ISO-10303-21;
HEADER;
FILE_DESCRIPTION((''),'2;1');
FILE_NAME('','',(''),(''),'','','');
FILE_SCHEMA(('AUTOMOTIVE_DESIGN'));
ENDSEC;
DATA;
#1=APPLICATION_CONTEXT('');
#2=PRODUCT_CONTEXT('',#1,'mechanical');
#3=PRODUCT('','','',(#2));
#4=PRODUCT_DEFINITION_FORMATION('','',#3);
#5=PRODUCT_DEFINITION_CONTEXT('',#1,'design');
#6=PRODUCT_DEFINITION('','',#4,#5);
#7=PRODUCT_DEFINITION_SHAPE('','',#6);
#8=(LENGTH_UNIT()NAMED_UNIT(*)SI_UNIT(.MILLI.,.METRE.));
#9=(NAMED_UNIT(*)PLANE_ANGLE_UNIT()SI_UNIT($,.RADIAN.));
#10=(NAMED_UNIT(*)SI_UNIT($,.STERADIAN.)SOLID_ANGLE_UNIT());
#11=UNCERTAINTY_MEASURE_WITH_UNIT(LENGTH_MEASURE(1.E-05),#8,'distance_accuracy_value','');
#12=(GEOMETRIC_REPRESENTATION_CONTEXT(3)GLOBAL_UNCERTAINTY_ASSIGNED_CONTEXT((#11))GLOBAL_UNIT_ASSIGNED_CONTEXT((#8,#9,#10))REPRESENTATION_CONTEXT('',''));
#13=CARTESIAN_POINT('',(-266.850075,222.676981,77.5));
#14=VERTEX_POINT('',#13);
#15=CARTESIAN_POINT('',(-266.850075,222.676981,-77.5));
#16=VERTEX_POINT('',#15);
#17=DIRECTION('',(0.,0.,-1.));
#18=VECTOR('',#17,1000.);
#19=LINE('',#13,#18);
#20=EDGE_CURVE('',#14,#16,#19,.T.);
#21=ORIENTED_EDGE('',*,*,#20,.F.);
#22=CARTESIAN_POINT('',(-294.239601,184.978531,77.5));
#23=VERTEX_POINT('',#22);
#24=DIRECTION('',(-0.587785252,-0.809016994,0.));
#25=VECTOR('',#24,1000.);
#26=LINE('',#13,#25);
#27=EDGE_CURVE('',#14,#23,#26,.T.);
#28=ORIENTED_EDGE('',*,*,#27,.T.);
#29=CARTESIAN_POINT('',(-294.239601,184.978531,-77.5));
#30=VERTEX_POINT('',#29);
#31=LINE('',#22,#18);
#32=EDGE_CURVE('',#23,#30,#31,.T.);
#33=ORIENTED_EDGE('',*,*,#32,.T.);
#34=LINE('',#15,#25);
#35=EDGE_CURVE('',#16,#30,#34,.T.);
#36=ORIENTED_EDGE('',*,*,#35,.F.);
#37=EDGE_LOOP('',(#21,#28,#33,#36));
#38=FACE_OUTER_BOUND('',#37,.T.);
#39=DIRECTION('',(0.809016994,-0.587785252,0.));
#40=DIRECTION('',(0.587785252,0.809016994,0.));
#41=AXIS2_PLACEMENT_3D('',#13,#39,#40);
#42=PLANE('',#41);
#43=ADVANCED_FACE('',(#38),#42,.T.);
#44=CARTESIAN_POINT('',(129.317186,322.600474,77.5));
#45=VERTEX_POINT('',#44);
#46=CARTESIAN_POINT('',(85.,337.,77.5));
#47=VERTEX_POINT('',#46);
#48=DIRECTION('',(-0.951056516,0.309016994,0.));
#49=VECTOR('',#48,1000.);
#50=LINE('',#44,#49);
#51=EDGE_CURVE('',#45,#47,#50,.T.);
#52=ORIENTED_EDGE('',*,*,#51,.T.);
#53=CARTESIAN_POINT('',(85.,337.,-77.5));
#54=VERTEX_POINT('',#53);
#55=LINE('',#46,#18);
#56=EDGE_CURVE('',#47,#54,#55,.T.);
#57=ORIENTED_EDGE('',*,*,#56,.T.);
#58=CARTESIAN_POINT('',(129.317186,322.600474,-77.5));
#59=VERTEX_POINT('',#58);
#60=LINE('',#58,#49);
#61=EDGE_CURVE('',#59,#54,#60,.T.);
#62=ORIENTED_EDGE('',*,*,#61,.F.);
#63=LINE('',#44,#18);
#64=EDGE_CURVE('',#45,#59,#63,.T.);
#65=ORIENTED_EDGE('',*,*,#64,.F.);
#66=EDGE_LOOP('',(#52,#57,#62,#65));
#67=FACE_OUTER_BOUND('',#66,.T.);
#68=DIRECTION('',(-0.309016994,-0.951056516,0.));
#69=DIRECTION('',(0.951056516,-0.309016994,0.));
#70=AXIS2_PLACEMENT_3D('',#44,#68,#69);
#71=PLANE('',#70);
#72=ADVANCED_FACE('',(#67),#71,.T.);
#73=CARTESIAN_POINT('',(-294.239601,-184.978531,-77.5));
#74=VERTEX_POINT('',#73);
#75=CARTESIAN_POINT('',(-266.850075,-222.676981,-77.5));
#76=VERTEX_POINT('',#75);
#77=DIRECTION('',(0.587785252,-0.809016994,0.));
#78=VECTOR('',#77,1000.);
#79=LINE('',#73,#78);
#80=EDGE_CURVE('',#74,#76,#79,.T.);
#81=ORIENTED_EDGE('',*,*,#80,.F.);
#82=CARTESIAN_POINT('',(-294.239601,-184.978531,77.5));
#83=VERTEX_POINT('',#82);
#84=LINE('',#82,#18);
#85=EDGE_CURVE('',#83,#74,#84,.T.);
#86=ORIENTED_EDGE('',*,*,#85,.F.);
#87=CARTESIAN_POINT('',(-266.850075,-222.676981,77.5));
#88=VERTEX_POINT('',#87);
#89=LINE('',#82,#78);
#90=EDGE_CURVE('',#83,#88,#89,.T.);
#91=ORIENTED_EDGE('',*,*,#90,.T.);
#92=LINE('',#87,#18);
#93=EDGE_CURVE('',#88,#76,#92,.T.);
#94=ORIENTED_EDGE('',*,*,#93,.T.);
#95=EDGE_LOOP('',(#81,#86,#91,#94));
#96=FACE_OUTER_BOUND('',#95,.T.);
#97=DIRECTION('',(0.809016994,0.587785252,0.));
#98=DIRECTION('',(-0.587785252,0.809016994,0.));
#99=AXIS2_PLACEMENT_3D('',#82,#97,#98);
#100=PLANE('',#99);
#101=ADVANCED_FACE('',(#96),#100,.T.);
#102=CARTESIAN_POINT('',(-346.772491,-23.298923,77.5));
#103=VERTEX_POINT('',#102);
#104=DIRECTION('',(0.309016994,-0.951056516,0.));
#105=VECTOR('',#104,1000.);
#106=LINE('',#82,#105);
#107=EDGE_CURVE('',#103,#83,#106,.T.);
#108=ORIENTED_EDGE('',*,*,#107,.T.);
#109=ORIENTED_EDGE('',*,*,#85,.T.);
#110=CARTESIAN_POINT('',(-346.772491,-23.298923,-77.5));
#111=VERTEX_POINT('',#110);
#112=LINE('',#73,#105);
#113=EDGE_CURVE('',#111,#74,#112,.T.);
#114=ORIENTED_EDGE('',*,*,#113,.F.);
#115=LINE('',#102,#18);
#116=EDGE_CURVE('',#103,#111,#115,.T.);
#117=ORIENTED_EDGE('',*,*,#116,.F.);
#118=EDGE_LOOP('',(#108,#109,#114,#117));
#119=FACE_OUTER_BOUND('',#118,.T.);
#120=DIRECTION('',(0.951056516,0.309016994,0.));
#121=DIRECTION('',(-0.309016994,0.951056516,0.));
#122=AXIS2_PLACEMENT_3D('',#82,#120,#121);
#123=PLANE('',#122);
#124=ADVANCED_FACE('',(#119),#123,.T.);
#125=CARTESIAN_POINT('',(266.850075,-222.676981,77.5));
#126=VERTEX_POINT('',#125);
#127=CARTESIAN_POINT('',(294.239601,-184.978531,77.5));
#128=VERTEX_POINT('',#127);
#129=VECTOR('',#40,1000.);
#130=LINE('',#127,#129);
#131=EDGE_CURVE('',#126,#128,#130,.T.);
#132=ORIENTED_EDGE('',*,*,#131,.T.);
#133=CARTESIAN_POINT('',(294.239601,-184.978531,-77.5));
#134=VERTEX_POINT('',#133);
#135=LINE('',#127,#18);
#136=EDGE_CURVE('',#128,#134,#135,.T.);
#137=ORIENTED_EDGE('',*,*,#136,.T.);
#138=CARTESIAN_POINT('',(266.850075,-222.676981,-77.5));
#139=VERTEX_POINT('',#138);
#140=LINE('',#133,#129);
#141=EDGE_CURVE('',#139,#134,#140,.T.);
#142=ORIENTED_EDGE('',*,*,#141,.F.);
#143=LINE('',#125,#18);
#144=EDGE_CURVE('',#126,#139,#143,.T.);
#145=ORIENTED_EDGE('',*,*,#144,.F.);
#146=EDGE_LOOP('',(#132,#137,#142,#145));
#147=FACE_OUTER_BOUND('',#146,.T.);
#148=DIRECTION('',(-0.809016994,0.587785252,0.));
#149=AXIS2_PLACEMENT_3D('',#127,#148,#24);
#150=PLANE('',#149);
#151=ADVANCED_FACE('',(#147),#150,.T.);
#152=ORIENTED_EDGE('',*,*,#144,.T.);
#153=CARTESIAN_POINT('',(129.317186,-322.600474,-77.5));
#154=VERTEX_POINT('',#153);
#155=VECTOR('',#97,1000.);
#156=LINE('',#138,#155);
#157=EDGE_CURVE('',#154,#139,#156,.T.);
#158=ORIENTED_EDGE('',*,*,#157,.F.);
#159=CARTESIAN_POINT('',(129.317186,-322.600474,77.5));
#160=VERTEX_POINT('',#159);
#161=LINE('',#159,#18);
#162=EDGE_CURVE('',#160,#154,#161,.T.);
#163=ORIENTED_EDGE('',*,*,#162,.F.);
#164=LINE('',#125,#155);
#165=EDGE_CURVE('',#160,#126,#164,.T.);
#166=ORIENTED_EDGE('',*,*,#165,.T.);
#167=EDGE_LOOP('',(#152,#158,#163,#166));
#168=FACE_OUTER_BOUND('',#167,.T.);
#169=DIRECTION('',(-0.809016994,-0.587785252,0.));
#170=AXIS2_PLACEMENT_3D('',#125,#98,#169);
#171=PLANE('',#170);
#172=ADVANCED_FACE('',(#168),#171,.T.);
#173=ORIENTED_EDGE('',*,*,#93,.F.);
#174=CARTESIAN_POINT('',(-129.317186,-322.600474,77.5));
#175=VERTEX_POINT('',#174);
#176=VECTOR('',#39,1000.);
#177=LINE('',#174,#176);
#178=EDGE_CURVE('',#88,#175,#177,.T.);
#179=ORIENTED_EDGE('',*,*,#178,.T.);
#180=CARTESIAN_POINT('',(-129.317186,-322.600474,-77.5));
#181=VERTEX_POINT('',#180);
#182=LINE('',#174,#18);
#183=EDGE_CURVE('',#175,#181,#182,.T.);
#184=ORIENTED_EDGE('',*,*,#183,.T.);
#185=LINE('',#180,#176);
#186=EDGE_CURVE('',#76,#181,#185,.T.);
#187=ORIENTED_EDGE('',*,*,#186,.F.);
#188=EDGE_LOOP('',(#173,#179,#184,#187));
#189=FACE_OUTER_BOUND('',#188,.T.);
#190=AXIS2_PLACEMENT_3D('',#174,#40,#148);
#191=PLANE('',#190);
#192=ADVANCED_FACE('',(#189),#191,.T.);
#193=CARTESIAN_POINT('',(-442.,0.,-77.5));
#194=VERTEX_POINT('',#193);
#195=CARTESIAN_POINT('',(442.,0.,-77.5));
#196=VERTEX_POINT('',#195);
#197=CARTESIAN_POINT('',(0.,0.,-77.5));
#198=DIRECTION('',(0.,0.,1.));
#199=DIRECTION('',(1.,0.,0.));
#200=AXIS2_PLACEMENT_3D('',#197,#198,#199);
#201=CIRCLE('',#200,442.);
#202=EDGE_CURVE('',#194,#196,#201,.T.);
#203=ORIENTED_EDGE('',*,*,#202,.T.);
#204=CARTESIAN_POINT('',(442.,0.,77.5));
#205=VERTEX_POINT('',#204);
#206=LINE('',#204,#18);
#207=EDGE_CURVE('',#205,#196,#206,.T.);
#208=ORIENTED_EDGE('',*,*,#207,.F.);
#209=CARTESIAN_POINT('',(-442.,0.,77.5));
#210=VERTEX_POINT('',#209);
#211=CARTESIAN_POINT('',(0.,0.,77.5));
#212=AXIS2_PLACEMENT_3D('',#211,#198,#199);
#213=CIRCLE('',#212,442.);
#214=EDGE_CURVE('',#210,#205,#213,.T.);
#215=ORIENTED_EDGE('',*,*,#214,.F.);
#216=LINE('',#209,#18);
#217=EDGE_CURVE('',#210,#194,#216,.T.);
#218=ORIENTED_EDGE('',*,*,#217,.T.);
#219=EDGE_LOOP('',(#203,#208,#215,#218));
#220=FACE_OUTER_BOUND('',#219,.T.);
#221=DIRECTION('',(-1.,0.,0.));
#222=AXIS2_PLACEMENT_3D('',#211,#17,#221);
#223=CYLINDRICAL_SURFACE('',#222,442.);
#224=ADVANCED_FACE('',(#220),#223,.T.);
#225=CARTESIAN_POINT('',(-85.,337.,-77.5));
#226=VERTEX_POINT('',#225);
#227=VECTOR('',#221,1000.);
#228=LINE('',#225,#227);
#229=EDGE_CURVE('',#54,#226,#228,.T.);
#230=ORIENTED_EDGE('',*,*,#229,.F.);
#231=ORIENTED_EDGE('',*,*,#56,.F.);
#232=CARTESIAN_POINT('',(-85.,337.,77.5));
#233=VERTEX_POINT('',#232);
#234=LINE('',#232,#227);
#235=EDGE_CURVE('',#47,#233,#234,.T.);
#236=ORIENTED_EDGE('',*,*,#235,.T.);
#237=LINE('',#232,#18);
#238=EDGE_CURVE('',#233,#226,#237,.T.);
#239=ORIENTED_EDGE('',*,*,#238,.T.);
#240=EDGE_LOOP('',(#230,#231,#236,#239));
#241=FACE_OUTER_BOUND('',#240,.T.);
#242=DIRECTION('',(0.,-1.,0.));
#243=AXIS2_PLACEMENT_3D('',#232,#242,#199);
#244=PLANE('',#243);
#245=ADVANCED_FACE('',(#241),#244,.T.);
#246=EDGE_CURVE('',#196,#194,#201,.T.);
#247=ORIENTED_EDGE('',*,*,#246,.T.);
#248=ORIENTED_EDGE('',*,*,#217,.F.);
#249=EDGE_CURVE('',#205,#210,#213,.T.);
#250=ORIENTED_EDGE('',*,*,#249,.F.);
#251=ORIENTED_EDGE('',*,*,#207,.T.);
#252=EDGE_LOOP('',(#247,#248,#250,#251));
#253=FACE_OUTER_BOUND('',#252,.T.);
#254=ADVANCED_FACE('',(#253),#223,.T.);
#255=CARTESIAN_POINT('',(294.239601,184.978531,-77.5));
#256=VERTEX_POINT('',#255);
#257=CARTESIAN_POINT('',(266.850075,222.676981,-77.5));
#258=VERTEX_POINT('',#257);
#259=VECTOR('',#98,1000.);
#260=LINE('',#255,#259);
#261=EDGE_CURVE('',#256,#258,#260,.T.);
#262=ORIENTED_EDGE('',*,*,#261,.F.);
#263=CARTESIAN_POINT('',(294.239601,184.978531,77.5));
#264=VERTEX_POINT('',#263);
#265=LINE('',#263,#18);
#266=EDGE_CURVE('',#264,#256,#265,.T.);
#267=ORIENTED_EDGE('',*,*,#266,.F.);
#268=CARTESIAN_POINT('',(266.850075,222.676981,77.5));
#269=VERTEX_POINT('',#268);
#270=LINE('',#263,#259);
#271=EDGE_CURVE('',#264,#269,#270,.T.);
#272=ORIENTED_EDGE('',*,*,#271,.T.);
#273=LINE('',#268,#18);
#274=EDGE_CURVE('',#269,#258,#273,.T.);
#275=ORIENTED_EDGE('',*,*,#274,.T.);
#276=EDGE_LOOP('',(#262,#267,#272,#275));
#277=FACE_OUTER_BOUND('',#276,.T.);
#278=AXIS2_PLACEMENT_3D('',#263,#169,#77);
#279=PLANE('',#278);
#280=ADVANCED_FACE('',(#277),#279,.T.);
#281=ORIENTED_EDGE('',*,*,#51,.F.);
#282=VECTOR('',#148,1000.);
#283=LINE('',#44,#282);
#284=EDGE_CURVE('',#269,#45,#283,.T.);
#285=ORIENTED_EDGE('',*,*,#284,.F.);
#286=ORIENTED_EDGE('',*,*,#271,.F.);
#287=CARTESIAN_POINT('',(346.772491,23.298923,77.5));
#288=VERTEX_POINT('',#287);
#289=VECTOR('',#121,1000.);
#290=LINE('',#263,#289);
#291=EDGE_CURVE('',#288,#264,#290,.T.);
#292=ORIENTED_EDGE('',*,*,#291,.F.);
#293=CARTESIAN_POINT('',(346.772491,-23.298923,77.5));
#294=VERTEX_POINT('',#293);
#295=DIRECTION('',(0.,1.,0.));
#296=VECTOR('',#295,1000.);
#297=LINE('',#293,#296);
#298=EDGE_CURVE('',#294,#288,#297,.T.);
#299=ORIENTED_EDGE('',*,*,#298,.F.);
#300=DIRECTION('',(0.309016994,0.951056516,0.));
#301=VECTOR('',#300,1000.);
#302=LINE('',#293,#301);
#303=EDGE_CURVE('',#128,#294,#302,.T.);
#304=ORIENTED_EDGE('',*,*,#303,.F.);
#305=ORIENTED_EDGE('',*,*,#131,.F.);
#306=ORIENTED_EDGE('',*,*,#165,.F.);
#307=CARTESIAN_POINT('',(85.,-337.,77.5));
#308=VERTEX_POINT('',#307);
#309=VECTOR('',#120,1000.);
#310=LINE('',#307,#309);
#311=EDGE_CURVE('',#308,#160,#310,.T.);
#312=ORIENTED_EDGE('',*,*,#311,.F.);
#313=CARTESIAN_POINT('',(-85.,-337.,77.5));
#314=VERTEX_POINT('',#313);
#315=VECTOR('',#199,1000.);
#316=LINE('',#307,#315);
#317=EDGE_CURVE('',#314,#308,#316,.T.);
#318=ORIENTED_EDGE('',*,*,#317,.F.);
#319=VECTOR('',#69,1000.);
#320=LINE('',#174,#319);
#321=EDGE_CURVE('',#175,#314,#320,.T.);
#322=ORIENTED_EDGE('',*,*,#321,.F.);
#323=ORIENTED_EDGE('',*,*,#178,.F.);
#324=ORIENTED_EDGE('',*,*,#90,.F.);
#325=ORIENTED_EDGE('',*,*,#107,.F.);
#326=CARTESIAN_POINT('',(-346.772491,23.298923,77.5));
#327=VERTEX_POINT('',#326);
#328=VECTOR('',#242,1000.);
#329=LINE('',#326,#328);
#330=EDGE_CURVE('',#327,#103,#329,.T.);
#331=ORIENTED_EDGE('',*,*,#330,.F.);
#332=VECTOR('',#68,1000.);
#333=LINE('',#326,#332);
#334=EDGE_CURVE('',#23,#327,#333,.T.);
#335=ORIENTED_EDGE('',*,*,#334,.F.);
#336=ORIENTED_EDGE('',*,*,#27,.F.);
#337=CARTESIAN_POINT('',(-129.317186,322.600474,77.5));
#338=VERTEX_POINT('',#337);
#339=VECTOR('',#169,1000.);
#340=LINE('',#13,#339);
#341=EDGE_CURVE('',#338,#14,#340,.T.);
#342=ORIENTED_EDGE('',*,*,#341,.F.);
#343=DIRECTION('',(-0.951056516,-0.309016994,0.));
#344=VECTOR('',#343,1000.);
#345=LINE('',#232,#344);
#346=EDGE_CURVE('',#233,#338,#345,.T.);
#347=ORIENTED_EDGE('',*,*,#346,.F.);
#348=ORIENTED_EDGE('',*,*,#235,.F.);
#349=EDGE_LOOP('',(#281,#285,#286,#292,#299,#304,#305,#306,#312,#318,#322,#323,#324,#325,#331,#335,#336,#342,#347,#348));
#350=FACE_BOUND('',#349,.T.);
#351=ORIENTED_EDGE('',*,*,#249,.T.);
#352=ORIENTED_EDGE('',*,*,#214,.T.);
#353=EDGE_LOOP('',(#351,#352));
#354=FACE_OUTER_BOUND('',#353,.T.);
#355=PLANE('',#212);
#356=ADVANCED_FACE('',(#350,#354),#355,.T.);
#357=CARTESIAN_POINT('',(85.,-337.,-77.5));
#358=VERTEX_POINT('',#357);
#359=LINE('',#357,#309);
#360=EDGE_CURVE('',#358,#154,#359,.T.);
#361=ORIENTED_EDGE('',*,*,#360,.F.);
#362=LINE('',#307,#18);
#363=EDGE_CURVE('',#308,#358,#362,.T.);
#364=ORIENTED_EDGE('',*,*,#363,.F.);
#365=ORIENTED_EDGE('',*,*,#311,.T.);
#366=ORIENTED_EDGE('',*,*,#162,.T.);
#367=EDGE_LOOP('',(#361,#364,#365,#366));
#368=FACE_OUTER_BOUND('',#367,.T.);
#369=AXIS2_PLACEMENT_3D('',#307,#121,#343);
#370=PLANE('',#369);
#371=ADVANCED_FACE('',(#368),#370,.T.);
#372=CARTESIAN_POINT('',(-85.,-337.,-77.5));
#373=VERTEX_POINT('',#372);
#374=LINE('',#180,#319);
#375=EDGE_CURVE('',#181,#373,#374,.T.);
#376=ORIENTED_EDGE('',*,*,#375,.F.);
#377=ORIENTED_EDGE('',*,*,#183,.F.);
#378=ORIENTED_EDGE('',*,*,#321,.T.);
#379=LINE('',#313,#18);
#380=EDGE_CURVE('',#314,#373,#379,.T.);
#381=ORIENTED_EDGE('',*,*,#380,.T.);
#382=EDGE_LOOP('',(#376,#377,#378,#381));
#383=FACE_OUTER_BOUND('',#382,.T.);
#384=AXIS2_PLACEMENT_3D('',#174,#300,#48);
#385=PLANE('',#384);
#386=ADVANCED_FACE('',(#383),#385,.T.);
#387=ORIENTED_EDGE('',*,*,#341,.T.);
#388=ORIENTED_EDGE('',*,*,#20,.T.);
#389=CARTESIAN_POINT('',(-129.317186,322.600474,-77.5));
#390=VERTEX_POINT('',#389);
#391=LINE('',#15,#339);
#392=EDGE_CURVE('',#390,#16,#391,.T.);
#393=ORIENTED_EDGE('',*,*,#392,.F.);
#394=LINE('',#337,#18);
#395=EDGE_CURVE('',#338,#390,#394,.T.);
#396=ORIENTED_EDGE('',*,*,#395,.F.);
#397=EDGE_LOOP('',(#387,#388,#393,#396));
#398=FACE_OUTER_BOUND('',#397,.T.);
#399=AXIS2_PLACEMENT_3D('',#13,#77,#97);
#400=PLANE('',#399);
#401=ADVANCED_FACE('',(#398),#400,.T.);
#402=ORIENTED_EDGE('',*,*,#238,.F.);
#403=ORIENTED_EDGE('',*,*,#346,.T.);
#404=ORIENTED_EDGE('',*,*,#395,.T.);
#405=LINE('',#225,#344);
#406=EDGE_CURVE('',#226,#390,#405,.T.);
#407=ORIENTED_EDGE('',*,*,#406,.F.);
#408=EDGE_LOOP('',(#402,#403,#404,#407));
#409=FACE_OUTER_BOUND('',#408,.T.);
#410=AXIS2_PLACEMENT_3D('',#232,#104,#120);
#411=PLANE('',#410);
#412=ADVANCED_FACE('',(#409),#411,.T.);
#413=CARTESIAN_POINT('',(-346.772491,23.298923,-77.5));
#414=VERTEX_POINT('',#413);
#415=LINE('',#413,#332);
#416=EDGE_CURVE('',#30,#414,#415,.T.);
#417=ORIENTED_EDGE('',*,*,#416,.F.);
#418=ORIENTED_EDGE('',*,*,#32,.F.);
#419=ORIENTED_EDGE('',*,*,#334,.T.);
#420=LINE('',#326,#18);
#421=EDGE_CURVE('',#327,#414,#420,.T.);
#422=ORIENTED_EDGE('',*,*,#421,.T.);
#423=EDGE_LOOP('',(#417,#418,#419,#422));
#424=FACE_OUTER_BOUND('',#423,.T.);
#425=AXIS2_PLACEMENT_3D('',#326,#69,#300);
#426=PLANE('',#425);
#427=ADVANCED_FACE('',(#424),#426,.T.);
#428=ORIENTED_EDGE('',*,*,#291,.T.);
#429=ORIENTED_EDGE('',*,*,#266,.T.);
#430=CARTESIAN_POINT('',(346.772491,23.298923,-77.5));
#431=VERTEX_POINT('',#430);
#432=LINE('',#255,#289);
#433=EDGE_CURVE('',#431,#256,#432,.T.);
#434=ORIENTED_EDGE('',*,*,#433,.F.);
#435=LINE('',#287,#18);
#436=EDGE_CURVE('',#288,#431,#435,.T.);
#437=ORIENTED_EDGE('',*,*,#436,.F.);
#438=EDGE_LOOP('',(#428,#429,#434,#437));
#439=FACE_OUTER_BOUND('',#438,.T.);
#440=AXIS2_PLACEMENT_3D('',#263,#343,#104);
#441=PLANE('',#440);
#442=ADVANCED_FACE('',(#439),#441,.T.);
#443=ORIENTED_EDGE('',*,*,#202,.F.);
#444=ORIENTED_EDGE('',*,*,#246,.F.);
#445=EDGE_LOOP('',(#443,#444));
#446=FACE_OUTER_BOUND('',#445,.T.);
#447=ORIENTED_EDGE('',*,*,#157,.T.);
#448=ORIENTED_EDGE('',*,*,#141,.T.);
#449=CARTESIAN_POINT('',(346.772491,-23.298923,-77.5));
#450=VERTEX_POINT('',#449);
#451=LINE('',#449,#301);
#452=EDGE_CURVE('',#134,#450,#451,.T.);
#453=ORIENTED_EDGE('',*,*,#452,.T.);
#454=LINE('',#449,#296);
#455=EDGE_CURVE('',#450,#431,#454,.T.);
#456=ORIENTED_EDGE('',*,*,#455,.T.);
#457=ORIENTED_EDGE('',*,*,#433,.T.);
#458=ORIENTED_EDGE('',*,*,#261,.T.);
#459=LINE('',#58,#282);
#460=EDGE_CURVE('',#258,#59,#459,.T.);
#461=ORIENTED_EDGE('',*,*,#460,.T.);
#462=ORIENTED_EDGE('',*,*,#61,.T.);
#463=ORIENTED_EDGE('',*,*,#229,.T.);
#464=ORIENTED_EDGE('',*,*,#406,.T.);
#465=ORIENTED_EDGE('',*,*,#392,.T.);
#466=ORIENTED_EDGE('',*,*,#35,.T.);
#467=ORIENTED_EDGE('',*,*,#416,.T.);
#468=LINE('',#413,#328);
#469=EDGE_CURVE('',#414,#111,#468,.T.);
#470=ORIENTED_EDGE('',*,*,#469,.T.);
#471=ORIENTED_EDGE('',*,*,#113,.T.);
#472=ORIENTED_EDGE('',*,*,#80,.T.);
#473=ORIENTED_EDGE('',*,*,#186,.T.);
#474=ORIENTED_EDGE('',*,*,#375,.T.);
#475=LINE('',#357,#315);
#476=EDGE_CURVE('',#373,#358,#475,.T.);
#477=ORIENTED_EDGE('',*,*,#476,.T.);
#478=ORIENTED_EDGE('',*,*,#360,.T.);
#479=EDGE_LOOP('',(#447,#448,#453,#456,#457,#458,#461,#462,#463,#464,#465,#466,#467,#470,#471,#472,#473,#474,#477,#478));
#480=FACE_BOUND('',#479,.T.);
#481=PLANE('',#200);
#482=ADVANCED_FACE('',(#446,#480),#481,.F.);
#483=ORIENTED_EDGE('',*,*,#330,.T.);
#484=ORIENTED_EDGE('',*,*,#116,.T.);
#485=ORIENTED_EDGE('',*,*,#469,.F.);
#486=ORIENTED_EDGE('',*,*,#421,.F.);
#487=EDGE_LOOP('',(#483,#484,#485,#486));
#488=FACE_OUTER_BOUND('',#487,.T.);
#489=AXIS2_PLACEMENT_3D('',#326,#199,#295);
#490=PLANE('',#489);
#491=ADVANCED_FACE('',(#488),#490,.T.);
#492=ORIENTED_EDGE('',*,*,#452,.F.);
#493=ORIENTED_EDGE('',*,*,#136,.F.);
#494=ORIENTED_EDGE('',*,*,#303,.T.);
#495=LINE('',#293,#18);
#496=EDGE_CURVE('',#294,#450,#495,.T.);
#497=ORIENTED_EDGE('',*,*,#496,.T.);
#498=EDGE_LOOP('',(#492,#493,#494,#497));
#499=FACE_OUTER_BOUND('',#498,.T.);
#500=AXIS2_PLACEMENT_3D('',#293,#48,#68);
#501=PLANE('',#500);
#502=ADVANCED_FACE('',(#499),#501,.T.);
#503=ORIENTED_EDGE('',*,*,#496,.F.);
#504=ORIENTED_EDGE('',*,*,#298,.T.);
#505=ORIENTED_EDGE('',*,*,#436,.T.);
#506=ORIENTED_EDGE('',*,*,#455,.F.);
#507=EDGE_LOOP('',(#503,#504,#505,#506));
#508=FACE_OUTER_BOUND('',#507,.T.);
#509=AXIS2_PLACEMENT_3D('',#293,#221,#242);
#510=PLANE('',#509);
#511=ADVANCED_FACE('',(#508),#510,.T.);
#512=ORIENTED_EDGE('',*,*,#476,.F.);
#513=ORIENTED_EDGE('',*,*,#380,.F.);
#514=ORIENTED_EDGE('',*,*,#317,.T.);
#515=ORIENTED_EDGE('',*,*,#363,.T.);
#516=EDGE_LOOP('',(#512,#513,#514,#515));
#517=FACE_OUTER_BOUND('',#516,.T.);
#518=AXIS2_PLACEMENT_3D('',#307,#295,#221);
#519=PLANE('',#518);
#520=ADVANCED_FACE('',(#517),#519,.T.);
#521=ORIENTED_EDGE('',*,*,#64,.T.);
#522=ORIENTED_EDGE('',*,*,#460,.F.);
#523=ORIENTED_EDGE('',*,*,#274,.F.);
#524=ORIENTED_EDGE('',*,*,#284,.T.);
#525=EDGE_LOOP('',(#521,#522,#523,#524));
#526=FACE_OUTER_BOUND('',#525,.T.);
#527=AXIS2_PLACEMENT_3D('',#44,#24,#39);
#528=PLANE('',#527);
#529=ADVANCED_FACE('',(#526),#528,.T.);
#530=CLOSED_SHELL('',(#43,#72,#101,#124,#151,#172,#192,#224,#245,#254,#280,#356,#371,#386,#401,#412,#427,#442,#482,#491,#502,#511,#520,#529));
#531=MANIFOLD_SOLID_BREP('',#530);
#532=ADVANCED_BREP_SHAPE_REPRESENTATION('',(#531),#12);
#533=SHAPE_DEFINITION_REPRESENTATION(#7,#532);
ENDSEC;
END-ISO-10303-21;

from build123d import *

# Parameters (mm, degrees)
SKETCH_1_R      = 442
EXTRUDE_1_DEPTH = 77.5


with BuildPart() as part:
    # 草图1 → 凸台-拉伸1 (new, symmetric)
    with BuildSketch(Plane.XY):
        Circle(SKETCH_1_R)
        Polygon((346.772490513, -23.298923219), (346.772490513, 23.298923219), (294.23960147, 184.978530989), (266.850074544, 222.676980659), (129.317185501, 322.600473549), (85, 337), (-85, 337), (-129.317185501, 322.600473549), (-266.850074544, 222.676980659), (-294.23960147, 184.978530989), (-346.772490513, 23.298923219), (-346.772490513, -23.298923219), (-294.23960147, -184.978530989), (-266.850074544, -222.676980659), (-129.317185501, -322.600473549), (-85, -337), (85, -337), (129.317185501, -322.600473549), (266.850074544, -222.67698066), (294.23960147, -184.978530989), align=None, mode=Mode.SUBTRACT)
    extrude(amount=EXTRUDE_1_DEPTH, both=True)


solid = part.part
